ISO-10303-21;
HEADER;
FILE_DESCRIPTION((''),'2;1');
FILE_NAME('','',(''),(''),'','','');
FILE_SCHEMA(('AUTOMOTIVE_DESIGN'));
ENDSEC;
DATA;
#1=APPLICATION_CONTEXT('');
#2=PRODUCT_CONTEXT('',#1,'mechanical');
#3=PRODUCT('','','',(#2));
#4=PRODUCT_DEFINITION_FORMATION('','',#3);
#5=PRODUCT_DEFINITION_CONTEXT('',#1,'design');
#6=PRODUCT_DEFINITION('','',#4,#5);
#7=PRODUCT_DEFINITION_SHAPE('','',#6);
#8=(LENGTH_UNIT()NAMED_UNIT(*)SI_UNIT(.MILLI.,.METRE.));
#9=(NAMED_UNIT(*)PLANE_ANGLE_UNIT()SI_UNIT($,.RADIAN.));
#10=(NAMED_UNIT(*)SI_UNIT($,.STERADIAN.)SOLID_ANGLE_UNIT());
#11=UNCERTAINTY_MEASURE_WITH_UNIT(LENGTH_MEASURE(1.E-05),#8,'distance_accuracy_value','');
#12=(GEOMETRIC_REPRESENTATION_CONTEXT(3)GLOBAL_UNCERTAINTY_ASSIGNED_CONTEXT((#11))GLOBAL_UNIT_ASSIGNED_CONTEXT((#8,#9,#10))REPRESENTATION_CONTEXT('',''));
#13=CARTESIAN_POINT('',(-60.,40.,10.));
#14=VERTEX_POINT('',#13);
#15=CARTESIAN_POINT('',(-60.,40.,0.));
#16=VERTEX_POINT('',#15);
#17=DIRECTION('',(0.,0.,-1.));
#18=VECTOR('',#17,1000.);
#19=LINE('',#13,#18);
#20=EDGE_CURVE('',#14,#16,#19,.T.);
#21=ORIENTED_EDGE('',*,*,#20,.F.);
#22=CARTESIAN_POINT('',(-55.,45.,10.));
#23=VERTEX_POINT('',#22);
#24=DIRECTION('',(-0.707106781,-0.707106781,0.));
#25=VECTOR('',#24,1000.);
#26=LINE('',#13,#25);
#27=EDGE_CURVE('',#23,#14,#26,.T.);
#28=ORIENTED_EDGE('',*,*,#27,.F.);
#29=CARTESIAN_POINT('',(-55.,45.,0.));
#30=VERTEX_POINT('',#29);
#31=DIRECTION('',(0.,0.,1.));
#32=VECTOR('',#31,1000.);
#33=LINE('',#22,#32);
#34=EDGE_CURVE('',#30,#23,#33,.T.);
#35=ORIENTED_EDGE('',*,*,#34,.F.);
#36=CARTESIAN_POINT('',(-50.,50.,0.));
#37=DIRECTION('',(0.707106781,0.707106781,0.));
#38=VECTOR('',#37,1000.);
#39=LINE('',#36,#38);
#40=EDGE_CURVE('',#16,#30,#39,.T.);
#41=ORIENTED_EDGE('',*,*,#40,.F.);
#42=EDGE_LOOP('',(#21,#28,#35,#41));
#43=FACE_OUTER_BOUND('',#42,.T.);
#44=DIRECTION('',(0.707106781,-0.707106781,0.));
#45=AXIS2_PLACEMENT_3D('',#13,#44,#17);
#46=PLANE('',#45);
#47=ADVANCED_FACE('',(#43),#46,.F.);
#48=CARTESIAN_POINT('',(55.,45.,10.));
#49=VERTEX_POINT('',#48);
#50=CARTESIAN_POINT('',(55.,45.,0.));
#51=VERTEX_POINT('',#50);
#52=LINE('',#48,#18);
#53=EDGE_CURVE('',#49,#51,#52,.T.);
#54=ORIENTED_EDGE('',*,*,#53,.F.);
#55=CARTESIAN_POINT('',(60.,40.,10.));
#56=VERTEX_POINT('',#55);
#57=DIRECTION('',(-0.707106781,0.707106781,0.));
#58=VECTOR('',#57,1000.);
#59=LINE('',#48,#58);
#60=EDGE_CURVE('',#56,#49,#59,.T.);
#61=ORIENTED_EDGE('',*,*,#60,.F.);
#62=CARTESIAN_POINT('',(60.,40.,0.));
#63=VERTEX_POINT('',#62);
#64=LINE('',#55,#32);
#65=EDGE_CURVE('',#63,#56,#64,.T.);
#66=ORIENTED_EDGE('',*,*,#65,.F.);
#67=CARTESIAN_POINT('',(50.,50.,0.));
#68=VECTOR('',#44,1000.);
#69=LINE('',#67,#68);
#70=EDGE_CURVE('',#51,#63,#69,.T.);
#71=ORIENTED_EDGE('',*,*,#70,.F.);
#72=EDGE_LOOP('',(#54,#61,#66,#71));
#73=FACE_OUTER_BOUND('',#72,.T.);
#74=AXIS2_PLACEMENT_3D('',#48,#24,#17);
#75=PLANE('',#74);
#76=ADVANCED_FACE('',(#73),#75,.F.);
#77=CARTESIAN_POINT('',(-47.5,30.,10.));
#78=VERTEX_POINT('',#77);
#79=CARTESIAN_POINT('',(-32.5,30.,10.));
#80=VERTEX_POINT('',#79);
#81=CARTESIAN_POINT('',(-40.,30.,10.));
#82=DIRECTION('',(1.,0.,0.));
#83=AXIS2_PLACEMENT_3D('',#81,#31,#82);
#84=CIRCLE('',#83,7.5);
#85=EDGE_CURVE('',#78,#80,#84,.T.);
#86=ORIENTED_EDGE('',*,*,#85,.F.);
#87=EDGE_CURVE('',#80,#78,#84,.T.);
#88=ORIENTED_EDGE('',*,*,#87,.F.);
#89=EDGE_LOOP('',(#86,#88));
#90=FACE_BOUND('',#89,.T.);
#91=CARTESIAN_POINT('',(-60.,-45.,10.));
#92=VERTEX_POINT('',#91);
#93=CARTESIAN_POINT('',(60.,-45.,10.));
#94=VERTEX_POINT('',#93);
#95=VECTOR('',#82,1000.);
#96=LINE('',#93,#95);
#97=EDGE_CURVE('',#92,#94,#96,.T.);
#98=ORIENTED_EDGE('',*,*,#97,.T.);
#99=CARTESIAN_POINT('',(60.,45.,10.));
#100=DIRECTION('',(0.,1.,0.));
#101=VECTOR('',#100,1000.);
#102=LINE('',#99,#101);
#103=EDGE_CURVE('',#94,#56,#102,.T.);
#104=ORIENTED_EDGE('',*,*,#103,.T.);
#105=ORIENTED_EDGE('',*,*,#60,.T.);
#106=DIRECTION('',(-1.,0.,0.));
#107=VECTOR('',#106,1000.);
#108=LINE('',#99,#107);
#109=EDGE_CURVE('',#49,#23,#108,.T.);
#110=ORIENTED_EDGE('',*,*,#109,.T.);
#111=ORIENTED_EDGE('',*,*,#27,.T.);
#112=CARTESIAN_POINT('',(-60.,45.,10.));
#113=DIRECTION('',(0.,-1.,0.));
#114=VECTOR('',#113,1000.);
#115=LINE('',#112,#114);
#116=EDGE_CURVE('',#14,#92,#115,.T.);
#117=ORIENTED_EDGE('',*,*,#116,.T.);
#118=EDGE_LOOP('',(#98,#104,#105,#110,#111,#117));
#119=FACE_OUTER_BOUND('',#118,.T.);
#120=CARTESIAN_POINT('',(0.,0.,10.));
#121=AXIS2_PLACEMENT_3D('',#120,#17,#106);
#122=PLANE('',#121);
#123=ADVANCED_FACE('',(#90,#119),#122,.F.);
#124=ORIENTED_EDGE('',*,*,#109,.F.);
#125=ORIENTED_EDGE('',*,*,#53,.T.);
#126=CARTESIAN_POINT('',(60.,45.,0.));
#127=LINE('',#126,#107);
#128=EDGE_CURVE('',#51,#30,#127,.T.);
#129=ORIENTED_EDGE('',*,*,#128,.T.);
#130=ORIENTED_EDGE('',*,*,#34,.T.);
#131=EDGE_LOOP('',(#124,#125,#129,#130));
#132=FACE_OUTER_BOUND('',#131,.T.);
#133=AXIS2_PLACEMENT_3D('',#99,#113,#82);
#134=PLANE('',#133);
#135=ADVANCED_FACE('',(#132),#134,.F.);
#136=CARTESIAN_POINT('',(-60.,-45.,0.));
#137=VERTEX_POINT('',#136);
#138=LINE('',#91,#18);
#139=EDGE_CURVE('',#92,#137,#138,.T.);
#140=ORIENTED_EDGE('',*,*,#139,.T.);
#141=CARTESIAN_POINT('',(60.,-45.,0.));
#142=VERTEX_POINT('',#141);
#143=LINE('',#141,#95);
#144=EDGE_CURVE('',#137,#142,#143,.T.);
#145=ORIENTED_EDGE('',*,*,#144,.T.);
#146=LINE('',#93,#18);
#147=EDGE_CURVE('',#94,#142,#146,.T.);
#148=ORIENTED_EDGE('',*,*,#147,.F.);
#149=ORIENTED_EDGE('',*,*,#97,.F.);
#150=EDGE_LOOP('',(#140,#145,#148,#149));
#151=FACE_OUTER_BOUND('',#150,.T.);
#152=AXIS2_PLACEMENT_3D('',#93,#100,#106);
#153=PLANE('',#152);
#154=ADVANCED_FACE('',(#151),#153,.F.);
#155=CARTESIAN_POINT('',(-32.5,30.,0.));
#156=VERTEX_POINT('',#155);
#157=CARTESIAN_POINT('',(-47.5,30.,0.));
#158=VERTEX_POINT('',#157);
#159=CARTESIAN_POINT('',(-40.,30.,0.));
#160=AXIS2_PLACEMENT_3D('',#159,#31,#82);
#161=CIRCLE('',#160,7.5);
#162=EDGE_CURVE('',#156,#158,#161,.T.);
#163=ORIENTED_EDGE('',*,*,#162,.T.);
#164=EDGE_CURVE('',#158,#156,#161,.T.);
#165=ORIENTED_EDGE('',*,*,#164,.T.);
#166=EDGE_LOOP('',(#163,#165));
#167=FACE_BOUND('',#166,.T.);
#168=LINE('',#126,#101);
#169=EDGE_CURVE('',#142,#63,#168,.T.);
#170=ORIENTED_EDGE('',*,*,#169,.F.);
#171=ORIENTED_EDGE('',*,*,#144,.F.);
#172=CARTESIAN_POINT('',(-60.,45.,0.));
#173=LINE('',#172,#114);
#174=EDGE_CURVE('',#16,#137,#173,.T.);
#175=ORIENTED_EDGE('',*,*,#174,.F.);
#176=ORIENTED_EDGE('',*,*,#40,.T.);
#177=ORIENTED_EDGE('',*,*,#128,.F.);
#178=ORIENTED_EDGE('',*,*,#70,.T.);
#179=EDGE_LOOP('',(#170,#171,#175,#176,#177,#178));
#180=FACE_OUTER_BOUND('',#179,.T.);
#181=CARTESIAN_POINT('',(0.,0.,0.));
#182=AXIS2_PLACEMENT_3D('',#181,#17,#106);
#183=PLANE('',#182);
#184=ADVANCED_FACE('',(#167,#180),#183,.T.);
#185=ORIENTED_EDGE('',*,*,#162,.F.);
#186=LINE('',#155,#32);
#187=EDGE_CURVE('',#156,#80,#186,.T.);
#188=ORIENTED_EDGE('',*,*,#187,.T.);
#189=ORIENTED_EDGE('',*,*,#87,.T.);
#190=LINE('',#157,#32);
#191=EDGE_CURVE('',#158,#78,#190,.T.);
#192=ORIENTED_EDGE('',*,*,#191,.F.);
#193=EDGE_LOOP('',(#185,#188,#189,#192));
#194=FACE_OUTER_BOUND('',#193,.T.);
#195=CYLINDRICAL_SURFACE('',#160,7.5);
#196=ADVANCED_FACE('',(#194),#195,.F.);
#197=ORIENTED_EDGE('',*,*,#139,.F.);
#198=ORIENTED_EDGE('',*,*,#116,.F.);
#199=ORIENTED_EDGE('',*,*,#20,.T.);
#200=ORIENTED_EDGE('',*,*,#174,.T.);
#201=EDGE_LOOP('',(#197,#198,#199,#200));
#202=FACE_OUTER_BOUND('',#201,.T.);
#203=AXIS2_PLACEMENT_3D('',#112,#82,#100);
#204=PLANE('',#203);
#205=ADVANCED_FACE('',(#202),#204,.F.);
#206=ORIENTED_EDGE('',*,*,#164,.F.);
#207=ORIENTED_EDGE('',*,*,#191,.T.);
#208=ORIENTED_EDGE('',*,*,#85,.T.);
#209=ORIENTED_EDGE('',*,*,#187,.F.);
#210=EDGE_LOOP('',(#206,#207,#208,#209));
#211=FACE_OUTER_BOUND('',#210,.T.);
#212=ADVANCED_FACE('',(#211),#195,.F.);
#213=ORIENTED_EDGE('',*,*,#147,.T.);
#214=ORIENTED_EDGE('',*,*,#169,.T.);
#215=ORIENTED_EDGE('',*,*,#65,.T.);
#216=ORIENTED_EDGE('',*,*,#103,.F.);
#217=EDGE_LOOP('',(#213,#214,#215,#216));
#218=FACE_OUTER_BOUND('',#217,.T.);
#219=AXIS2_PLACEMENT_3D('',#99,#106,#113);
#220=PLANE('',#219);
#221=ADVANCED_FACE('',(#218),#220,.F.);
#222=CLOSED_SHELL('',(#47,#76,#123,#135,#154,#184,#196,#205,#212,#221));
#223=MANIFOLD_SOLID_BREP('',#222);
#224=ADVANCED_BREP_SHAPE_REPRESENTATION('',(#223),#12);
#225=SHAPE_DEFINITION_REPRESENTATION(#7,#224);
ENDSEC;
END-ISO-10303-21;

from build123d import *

# Parameters (mm, degrees)
SKETCH1_W           = 120
SKETCH1_H           = 90
BOSS_EXTRUDE1_DEPTH = 10
SKETCH2_R           = 7.5
CUT_EXTRUDE1_DEPTH  = 10
CHAMFER1_SIZE       = 5


with BuildPart() as part:
    # Sketch1 → Boss-Extrude1 (new body)
    with BuildSketch(Plane.XY):
        Rectangle(SKETCH1_W, SKETCH1_H)
    extrude(amount=BOSS_EXTRUDE1_DEPTH)

    # Sketch2 → Cut-Extrude1 (cut)
    with BuildSketch(Plane.XY.offset(10)):
        with Locations((-40, 30)):
            Circle(SKETCH2_R)
    extrude(amount=-CUT_EXTRUDE1_DEPTH, mode=Mode.SUBTRACT)

    # Chamfer1
    chamfer1_edges = [part.edges().sort_by_distance(p)[0] for p in [
        (-60, 45, 5),
        (60, 45, 5),
    ]]
    chamfer(chamfer1_edges, length=CHAMFER1_SIZE)


solid = part.part
